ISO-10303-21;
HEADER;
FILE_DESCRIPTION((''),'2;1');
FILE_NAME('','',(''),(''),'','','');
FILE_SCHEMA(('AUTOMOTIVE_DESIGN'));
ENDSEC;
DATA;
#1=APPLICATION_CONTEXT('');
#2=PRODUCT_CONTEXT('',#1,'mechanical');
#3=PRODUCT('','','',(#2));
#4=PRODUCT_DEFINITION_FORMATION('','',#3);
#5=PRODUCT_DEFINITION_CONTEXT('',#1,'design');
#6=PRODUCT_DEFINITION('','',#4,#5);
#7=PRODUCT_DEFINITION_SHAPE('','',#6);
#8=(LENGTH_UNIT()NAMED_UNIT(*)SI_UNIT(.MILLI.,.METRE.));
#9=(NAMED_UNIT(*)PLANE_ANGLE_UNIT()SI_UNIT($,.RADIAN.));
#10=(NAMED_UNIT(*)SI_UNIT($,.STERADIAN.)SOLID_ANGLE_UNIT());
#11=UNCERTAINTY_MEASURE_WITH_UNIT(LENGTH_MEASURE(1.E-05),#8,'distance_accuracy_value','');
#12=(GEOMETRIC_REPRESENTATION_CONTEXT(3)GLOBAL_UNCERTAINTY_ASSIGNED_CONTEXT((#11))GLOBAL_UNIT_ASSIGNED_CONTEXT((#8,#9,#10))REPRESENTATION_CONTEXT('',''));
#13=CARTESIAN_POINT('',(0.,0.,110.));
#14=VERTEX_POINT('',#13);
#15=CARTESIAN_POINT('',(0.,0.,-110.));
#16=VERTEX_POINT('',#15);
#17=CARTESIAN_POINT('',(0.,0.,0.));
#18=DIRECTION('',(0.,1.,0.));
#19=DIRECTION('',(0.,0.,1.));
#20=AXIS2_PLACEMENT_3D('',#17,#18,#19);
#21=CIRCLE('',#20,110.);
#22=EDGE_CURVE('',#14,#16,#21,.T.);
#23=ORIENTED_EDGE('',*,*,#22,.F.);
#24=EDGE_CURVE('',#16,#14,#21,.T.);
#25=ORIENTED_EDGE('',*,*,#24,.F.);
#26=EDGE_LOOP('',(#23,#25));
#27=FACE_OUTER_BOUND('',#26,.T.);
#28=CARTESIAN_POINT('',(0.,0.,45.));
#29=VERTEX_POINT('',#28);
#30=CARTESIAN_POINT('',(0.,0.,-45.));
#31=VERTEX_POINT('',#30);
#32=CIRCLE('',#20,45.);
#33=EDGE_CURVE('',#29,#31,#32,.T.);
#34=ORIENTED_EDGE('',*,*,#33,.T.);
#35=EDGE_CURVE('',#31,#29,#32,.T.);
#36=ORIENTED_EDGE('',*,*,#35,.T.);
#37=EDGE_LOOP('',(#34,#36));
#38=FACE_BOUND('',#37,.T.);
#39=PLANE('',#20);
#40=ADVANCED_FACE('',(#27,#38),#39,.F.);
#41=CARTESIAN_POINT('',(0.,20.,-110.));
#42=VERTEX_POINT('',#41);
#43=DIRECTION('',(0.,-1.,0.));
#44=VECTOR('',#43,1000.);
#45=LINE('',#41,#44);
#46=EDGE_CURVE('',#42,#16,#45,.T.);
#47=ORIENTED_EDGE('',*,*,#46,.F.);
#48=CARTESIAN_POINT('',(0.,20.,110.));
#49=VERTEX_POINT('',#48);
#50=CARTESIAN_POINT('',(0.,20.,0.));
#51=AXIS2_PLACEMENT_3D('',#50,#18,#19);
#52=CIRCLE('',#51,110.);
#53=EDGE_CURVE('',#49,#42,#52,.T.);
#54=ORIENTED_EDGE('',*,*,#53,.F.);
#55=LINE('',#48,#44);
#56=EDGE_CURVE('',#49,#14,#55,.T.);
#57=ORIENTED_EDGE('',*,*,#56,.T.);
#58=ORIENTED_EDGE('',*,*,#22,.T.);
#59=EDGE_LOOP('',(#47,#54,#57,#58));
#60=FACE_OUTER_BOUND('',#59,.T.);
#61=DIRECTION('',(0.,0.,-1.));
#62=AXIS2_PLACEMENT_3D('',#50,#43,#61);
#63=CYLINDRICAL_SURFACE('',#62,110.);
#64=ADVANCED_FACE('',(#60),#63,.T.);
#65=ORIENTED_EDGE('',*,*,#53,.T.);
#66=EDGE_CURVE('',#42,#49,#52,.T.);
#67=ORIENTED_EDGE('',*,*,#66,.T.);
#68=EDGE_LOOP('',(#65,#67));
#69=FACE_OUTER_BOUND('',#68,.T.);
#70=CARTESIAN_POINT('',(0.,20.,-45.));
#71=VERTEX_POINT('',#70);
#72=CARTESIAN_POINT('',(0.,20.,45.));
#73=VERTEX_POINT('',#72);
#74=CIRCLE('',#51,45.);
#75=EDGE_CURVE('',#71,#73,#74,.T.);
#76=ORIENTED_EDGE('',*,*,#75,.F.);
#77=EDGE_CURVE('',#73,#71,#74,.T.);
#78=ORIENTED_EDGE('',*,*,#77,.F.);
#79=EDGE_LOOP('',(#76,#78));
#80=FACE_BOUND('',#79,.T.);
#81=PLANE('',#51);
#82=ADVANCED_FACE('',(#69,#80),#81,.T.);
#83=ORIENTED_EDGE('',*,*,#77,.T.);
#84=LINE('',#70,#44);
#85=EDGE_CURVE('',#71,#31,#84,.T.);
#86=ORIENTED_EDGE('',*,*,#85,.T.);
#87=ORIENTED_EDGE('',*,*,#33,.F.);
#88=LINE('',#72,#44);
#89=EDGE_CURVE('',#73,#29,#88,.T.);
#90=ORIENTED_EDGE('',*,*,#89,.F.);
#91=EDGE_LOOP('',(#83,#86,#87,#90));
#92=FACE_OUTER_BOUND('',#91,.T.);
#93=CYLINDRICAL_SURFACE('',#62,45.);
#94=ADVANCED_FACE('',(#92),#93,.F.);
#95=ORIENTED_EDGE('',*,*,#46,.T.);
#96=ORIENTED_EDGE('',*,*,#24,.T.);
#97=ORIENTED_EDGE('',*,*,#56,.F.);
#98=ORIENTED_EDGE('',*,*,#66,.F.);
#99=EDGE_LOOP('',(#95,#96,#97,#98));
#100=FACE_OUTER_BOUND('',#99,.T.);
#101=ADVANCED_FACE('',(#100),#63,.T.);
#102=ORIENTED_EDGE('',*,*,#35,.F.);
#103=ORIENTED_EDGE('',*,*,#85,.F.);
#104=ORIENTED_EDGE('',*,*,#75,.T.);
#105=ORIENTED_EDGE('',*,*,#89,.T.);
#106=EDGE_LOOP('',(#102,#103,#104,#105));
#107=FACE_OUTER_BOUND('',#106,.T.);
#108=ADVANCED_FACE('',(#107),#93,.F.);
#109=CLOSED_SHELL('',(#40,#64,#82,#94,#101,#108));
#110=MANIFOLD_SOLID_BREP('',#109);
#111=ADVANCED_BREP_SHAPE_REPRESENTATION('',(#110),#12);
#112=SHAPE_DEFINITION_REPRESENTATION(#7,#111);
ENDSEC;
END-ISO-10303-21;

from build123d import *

# Parameters (mm, degrees)
SKETCH_1_R      = 110
SKETCH_1_R_2    = 45
EXTRUDE_1_DEPTH = 20


with BuildPart() as part:
    # 草图1 → 凸台-拉伸1 (new body)
    with BuildSketch(Plane(origin=(0, 0, 0), x_dir=(1, 0, 0), z_dir=(0, 1, 0))):
        with Locations(Location((0, 0, 0), (0, 0, 270))):
            Circle(SKETCH_1_R)
        with Locations(Location((0, 0, 0), (0, 0, 270))):
            Circle(SKETCH_1_R_2, mode=Mode.SUBTRACT)
    extrude(amount=EXTRUDE_1_DEPTH)


solid = part.part
